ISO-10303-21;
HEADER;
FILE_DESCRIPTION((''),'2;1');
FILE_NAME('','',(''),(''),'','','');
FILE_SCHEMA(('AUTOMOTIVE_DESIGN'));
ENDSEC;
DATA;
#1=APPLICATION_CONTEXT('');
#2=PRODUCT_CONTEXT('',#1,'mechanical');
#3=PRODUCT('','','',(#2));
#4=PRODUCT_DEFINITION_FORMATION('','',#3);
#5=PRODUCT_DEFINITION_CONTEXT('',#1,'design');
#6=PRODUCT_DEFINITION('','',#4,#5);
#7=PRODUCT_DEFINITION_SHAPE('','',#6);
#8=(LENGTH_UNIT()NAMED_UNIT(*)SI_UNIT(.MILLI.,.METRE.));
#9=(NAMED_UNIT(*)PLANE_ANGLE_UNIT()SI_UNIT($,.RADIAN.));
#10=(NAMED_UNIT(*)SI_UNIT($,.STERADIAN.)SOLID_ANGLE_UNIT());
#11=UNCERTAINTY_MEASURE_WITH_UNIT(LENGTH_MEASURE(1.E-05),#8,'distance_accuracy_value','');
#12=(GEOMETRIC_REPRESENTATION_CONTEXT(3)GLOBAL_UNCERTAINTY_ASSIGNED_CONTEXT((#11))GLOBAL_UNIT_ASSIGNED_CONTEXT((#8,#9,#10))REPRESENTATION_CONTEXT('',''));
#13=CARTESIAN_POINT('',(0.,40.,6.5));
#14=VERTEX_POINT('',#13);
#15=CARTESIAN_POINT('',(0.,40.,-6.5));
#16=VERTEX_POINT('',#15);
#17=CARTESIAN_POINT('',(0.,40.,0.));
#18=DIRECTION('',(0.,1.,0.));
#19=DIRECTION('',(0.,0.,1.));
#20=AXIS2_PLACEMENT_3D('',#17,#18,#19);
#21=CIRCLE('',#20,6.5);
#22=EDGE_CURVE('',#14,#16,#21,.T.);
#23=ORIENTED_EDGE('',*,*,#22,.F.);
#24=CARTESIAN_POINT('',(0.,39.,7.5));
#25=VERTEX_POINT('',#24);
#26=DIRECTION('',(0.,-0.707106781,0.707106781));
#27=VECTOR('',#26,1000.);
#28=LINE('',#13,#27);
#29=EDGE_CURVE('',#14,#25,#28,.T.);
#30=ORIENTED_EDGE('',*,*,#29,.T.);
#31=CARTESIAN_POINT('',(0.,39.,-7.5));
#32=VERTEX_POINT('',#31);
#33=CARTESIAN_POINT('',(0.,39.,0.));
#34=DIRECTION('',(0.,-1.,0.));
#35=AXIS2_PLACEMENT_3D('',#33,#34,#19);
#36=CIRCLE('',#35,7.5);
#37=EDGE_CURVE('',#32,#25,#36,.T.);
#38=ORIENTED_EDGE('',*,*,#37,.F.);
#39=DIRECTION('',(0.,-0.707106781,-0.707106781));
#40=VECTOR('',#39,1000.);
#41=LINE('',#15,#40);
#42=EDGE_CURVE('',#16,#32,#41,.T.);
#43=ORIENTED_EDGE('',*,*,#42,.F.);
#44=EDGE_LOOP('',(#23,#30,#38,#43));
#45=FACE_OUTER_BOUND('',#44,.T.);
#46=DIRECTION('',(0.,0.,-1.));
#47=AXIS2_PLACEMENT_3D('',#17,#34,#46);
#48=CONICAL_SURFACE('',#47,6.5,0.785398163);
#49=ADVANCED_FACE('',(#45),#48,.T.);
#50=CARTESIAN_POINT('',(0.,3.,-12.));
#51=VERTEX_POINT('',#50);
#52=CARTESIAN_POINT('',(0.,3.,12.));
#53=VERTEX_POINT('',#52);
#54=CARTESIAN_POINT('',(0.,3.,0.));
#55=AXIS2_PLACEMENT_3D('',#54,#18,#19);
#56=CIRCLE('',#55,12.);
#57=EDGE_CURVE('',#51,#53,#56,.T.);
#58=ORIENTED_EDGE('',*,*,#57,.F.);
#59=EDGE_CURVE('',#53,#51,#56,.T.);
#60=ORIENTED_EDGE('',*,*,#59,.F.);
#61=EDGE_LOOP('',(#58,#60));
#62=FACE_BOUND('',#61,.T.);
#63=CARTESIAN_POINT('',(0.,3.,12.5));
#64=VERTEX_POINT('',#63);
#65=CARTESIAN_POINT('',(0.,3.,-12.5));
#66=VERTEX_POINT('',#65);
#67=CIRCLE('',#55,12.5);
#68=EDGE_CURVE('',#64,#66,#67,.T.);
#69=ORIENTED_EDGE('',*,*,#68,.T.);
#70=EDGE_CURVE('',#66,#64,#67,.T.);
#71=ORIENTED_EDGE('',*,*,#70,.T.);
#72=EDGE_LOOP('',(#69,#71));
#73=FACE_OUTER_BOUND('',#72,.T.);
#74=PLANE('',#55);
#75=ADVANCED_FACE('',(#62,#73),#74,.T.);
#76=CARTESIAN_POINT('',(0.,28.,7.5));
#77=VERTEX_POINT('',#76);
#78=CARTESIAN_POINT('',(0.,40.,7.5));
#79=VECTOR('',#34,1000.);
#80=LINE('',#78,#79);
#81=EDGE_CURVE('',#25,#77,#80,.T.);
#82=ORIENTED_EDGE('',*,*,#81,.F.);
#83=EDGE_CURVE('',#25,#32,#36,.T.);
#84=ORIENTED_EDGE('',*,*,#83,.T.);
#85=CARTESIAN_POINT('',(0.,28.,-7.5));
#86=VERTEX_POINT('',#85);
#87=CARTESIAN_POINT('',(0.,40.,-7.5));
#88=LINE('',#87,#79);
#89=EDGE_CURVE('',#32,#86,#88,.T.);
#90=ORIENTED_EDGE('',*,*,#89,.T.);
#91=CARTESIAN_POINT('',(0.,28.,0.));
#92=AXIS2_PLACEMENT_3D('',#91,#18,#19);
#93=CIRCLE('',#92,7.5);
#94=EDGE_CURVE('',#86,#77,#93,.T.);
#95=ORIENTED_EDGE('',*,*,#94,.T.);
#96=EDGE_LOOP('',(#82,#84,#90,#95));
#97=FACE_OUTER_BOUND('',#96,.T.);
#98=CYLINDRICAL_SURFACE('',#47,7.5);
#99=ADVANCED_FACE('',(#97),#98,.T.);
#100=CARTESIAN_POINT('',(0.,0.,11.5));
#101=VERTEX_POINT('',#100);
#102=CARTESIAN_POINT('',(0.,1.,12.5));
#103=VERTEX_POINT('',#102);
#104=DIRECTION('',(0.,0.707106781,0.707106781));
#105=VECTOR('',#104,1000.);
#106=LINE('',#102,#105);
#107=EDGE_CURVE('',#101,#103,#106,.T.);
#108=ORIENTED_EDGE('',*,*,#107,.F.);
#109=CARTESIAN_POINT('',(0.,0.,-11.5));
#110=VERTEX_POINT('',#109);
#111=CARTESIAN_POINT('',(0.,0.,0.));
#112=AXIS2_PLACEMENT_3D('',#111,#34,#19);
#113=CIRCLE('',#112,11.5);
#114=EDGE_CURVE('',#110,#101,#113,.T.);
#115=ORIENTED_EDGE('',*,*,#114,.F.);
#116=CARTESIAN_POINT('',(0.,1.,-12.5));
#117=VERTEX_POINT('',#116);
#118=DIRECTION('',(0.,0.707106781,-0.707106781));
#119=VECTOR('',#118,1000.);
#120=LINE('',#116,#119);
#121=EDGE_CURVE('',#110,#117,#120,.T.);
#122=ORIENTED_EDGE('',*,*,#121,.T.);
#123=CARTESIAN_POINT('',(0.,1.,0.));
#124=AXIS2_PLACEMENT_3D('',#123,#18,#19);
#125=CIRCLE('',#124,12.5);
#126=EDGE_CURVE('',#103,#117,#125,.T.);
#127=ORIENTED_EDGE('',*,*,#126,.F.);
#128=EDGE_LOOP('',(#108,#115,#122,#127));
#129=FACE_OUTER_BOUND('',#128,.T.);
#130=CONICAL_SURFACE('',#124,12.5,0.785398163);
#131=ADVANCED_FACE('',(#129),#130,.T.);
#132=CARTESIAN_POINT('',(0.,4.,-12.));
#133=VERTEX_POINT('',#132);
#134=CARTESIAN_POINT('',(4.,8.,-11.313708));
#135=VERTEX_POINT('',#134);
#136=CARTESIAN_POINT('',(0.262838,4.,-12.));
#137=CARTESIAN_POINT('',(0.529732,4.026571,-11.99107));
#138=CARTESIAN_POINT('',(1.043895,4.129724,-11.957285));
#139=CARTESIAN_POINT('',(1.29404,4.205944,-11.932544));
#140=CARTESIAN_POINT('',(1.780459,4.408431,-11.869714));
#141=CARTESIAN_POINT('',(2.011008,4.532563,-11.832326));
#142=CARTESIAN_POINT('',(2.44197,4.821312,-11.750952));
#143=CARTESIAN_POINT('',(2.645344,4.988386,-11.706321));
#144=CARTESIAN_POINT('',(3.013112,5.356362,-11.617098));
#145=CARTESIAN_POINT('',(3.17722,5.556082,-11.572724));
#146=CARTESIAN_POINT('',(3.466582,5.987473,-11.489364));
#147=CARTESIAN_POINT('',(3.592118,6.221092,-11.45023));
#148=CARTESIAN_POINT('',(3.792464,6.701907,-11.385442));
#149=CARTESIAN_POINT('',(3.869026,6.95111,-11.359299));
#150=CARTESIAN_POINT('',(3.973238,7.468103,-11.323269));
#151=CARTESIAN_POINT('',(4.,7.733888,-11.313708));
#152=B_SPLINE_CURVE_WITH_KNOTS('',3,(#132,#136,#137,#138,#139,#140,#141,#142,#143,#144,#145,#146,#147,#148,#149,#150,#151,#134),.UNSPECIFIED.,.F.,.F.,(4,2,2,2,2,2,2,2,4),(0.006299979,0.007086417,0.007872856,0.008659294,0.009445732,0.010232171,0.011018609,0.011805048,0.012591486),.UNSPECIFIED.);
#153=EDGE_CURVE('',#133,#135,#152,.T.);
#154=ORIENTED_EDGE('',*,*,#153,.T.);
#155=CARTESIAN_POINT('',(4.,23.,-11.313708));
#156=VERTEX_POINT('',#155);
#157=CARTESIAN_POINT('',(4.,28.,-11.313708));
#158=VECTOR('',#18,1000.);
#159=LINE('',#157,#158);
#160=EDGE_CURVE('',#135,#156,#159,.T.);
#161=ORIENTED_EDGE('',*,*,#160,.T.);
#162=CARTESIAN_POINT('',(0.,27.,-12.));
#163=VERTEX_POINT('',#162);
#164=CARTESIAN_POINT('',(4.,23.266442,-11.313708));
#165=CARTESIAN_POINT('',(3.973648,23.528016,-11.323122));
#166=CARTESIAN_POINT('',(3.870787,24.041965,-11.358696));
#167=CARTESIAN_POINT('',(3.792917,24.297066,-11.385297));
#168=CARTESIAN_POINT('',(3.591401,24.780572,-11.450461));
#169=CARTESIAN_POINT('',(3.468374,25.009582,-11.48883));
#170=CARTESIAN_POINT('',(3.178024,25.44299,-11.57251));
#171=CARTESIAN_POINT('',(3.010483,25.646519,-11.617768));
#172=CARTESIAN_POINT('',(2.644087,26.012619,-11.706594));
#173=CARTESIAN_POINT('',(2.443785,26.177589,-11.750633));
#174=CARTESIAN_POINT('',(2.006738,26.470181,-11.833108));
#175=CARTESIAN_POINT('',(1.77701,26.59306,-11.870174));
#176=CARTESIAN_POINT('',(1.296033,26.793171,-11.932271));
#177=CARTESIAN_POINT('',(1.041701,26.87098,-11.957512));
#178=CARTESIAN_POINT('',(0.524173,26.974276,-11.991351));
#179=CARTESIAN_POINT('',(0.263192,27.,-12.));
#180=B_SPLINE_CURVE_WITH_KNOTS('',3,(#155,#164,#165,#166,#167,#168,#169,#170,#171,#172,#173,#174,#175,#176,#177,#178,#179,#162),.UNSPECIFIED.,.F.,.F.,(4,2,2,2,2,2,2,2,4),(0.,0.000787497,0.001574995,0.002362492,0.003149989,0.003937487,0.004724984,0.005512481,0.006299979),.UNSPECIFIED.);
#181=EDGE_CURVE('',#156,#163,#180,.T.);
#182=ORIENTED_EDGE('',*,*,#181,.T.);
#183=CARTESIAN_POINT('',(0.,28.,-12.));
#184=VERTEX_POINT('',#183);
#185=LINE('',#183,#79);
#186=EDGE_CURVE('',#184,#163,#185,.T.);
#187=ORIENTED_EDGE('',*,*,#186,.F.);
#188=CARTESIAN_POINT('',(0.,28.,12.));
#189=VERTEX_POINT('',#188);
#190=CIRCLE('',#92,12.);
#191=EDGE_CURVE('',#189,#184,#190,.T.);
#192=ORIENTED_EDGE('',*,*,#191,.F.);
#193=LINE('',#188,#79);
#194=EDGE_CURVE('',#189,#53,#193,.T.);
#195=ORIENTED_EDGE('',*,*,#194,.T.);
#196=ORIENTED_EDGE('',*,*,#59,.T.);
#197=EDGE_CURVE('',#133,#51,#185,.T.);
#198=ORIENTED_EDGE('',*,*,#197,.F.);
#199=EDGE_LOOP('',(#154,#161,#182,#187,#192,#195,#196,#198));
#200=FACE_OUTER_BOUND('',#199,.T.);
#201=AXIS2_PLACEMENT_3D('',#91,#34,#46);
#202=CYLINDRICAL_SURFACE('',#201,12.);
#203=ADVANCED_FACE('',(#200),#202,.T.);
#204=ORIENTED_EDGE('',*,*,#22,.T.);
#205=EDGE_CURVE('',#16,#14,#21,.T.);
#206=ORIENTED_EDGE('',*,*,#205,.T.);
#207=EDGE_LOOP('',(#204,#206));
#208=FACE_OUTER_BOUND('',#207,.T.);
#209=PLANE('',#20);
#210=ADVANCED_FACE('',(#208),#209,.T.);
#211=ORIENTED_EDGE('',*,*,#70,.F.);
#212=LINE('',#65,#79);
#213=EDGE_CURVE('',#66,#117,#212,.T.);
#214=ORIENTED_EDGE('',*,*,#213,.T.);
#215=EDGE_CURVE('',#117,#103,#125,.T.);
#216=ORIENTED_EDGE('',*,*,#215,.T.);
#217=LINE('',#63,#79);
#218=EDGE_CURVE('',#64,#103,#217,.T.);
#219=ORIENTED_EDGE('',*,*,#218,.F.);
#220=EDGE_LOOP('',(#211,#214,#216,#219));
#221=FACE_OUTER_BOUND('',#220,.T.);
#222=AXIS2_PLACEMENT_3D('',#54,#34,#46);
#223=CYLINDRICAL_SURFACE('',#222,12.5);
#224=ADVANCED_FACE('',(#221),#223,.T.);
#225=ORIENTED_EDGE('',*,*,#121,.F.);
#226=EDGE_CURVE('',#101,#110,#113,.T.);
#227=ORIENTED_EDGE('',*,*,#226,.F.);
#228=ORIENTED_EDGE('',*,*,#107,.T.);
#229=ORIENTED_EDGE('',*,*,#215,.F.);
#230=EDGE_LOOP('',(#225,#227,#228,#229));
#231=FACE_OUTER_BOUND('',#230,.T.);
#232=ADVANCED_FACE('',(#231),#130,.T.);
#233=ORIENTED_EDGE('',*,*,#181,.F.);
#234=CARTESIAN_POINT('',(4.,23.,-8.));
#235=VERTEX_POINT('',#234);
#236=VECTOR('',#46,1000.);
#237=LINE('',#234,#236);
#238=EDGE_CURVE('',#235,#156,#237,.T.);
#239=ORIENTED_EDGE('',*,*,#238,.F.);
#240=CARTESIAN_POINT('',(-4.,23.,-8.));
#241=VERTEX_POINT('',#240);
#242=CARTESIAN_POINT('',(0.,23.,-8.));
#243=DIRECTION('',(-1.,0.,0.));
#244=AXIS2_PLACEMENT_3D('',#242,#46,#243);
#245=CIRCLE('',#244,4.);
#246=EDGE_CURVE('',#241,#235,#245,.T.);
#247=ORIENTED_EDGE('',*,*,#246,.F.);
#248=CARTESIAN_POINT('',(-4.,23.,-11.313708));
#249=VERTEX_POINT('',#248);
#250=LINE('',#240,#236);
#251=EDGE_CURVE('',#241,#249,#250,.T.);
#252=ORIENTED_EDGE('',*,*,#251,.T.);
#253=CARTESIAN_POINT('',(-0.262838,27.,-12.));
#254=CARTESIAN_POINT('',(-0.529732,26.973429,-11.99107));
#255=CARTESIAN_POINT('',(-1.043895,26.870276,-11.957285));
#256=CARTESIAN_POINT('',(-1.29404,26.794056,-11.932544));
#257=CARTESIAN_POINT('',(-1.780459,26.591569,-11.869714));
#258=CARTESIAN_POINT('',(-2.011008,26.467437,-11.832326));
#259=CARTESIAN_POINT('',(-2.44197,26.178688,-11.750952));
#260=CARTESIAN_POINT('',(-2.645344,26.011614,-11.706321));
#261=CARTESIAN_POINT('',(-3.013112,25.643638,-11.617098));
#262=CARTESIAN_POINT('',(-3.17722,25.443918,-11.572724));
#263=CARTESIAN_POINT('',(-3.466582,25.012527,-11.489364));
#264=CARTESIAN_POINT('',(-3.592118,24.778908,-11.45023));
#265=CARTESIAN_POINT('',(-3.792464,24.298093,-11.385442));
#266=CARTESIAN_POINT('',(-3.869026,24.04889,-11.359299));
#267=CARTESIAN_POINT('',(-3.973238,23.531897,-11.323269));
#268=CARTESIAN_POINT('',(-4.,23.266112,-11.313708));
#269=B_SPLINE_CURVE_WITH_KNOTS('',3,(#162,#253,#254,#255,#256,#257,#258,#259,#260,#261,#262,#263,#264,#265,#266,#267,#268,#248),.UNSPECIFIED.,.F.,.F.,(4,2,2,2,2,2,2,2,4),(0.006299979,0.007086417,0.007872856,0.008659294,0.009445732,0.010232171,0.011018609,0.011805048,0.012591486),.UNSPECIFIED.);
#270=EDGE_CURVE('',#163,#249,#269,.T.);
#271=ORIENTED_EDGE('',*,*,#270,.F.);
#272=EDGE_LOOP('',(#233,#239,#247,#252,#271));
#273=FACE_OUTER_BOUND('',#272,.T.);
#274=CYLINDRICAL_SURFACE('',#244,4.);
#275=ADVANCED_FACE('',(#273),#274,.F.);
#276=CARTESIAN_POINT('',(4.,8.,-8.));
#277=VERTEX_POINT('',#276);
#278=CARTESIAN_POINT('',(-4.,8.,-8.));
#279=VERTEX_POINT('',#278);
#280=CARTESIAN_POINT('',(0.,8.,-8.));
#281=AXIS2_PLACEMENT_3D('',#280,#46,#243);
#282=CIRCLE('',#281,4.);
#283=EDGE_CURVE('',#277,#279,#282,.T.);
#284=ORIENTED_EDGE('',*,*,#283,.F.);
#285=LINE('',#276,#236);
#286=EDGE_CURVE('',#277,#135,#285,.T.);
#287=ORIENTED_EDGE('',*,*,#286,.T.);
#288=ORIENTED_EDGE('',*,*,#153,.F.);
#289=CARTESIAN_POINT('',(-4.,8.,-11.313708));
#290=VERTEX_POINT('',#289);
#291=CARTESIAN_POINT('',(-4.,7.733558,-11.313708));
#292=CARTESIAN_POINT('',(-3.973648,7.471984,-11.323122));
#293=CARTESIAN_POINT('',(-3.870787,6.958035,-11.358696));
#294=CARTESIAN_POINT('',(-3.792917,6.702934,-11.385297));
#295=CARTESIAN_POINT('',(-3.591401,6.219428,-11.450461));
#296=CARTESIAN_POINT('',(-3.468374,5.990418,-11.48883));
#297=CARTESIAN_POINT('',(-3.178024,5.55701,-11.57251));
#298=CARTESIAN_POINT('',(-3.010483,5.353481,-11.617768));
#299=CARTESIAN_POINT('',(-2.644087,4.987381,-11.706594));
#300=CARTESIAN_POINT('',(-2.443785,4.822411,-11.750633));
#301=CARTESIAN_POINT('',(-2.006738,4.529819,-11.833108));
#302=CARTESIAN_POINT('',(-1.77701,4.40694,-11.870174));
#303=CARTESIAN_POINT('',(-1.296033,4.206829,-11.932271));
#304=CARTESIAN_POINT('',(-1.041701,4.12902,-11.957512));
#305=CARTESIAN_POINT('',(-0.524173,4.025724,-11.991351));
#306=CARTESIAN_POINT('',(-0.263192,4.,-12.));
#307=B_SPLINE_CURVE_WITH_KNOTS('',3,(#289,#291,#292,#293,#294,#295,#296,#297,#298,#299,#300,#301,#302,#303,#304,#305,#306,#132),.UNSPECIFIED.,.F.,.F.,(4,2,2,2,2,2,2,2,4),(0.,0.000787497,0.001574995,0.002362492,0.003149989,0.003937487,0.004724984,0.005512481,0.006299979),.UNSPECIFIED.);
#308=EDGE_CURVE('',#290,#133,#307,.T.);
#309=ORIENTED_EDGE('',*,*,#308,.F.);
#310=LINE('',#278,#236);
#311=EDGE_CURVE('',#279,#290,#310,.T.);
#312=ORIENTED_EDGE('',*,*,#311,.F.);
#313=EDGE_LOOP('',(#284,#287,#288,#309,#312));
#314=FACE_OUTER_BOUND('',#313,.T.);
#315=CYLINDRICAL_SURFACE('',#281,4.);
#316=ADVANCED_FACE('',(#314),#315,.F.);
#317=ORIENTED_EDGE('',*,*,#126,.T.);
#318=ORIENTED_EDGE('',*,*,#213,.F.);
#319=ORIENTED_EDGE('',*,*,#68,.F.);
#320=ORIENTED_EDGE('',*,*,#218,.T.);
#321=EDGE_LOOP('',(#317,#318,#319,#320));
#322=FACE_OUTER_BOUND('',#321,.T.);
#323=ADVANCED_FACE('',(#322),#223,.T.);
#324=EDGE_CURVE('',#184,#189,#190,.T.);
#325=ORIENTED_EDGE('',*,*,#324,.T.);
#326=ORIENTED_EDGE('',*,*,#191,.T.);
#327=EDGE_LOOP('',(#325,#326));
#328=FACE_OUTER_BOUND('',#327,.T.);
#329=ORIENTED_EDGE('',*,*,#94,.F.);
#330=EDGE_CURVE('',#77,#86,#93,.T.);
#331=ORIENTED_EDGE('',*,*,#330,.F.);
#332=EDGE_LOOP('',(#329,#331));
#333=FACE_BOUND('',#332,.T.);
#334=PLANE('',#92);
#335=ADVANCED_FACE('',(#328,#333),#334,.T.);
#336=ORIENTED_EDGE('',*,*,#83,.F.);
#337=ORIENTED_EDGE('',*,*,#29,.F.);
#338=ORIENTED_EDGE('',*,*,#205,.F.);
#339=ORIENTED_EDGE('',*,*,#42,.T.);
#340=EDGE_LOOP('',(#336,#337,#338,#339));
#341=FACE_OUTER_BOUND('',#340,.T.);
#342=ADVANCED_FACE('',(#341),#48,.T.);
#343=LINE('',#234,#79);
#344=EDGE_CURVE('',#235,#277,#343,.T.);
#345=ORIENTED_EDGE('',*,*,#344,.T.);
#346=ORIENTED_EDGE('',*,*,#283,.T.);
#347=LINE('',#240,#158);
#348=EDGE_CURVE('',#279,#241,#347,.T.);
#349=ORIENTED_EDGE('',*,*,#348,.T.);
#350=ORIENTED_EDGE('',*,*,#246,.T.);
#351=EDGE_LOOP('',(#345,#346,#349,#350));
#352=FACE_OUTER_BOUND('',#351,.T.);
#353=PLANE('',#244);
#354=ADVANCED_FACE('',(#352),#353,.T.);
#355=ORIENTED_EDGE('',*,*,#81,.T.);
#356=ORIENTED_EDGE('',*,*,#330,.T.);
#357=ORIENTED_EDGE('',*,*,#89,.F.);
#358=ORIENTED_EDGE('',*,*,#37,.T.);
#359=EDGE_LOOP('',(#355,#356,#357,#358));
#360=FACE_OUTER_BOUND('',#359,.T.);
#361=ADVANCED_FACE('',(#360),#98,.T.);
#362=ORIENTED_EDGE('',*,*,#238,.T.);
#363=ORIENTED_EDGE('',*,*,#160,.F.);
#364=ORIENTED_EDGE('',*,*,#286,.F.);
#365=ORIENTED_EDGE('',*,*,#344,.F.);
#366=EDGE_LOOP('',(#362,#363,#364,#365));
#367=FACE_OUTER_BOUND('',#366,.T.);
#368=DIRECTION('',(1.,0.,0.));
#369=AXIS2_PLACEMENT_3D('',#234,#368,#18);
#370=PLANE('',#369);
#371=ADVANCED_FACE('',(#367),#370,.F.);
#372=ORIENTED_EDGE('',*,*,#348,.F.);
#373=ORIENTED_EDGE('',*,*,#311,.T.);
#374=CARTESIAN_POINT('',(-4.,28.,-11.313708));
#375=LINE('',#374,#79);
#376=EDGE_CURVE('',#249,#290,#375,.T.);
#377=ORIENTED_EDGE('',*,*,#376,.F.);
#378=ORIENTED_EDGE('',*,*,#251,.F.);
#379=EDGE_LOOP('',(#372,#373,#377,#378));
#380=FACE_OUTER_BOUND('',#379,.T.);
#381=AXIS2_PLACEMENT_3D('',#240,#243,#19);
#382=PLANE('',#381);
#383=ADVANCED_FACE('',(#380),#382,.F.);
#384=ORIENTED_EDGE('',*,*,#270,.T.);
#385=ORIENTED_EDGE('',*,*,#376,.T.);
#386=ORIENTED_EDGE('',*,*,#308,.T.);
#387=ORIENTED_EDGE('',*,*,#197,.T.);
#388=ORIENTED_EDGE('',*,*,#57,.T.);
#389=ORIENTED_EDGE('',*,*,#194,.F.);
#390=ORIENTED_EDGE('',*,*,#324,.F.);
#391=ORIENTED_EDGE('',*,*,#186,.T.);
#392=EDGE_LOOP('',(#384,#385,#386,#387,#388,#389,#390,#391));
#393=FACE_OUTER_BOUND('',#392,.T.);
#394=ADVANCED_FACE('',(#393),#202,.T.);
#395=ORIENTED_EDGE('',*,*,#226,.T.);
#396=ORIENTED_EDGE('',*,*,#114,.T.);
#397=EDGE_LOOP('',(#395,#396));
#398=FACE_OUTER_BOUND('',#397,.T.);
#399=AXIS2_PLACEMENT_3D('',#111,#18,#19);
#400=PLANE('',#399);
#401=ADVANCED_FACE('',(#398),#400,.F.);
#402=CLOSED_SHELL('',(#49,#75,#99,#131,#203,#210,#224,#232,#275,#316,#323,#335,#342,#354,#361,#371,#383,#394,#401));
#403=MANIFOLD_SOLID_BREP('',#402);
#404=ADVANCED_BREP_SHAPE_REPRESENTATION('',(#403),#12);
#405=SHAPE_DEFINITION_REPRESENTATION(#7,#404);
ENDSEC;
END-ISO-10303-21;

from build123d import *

# Parameters (mm, degrees)
SKETCH1_R           = 12.5
BOSS_EXTRUDE1_DEPTH = 3
SKETCH2_R           = 12
BOSS_EXTRUDE2_DEPTH = 25
SKETCH3_R           = 7.5
BOSS_EXTRUDE3_DEPTH = 12
CUT_EXTRUDE1_DEPTH  = 4
CHAMFER1_SIZE       = 1


with BuildPart() as part:
    # Sketch1 → Boss-Extrude1 (new body)
    with BuildSketch(Plane(origin=(0, 0, 0), x_dir=(1, 0, 0), z_dir=(0, 1, 0))):
        with Locations(Location((0, 0, 0), (0, 0, 270))):
            Circle(SKETCH1_R)
    extrude(amount=BOSS_EXTRUDE1_DEPTH)

    # Sketch2 → Boss-Extrude2 (add)
    with BuildSketch(Plane(origin=(0, 3, 0), x_dir=(1, 0, 0), z_dir=(0, 1, 0))):
        with Locations(Location((0, 0, 0), (0, 0, 270))):
            Circle(SKETCH2_R)
    extrude(amount=BOSS_EXTRUDE2_DEPTH)

    # Sketch3 → Boss-Extrude3 (add)
    with BuildSketch(Plane(origin=(0, 28, 0), x_dir=(1, 0, 0), z_dir=(0, 1, 0))):
        with Locations(Location((0, 0, 0), (0, 0, 270))):
            Circle(SKETCH3_R)
    extrude(amount=BOSS_EXTRUDE3_DEPTH)

    # Sketch4 → Cut-Extrude1 (cut)
    with BuildSketch(Plane(origin=(0, 0, -12), x_dir=(-1, 0, 0), z_dir=(0, 0, -1))):
        with BuildLine():
            Line((4, 23), (4, 8))
            ThreePointArc((4, 8), (0, 4), (-4, 8))
            Line((-4, 8), (-4, 23))
            ThreePointArc((-4, 23), (0, 27), (4, 23))
        make_face()
    extrude(amount=-CUT_EXTRUDE1_DEPTH, mode=Mode.SUBTRACT)

    # Chamfer1
    chamfer1_edges = [part.edges().sort_by_distance(p)[0] for p in [
        (0, 40, -7.5),
        (0, 0, -12.5),
    ]]
    chamfer(chamfer1_edges, length=CHAMFER1_SIZE)


solid = part.part
